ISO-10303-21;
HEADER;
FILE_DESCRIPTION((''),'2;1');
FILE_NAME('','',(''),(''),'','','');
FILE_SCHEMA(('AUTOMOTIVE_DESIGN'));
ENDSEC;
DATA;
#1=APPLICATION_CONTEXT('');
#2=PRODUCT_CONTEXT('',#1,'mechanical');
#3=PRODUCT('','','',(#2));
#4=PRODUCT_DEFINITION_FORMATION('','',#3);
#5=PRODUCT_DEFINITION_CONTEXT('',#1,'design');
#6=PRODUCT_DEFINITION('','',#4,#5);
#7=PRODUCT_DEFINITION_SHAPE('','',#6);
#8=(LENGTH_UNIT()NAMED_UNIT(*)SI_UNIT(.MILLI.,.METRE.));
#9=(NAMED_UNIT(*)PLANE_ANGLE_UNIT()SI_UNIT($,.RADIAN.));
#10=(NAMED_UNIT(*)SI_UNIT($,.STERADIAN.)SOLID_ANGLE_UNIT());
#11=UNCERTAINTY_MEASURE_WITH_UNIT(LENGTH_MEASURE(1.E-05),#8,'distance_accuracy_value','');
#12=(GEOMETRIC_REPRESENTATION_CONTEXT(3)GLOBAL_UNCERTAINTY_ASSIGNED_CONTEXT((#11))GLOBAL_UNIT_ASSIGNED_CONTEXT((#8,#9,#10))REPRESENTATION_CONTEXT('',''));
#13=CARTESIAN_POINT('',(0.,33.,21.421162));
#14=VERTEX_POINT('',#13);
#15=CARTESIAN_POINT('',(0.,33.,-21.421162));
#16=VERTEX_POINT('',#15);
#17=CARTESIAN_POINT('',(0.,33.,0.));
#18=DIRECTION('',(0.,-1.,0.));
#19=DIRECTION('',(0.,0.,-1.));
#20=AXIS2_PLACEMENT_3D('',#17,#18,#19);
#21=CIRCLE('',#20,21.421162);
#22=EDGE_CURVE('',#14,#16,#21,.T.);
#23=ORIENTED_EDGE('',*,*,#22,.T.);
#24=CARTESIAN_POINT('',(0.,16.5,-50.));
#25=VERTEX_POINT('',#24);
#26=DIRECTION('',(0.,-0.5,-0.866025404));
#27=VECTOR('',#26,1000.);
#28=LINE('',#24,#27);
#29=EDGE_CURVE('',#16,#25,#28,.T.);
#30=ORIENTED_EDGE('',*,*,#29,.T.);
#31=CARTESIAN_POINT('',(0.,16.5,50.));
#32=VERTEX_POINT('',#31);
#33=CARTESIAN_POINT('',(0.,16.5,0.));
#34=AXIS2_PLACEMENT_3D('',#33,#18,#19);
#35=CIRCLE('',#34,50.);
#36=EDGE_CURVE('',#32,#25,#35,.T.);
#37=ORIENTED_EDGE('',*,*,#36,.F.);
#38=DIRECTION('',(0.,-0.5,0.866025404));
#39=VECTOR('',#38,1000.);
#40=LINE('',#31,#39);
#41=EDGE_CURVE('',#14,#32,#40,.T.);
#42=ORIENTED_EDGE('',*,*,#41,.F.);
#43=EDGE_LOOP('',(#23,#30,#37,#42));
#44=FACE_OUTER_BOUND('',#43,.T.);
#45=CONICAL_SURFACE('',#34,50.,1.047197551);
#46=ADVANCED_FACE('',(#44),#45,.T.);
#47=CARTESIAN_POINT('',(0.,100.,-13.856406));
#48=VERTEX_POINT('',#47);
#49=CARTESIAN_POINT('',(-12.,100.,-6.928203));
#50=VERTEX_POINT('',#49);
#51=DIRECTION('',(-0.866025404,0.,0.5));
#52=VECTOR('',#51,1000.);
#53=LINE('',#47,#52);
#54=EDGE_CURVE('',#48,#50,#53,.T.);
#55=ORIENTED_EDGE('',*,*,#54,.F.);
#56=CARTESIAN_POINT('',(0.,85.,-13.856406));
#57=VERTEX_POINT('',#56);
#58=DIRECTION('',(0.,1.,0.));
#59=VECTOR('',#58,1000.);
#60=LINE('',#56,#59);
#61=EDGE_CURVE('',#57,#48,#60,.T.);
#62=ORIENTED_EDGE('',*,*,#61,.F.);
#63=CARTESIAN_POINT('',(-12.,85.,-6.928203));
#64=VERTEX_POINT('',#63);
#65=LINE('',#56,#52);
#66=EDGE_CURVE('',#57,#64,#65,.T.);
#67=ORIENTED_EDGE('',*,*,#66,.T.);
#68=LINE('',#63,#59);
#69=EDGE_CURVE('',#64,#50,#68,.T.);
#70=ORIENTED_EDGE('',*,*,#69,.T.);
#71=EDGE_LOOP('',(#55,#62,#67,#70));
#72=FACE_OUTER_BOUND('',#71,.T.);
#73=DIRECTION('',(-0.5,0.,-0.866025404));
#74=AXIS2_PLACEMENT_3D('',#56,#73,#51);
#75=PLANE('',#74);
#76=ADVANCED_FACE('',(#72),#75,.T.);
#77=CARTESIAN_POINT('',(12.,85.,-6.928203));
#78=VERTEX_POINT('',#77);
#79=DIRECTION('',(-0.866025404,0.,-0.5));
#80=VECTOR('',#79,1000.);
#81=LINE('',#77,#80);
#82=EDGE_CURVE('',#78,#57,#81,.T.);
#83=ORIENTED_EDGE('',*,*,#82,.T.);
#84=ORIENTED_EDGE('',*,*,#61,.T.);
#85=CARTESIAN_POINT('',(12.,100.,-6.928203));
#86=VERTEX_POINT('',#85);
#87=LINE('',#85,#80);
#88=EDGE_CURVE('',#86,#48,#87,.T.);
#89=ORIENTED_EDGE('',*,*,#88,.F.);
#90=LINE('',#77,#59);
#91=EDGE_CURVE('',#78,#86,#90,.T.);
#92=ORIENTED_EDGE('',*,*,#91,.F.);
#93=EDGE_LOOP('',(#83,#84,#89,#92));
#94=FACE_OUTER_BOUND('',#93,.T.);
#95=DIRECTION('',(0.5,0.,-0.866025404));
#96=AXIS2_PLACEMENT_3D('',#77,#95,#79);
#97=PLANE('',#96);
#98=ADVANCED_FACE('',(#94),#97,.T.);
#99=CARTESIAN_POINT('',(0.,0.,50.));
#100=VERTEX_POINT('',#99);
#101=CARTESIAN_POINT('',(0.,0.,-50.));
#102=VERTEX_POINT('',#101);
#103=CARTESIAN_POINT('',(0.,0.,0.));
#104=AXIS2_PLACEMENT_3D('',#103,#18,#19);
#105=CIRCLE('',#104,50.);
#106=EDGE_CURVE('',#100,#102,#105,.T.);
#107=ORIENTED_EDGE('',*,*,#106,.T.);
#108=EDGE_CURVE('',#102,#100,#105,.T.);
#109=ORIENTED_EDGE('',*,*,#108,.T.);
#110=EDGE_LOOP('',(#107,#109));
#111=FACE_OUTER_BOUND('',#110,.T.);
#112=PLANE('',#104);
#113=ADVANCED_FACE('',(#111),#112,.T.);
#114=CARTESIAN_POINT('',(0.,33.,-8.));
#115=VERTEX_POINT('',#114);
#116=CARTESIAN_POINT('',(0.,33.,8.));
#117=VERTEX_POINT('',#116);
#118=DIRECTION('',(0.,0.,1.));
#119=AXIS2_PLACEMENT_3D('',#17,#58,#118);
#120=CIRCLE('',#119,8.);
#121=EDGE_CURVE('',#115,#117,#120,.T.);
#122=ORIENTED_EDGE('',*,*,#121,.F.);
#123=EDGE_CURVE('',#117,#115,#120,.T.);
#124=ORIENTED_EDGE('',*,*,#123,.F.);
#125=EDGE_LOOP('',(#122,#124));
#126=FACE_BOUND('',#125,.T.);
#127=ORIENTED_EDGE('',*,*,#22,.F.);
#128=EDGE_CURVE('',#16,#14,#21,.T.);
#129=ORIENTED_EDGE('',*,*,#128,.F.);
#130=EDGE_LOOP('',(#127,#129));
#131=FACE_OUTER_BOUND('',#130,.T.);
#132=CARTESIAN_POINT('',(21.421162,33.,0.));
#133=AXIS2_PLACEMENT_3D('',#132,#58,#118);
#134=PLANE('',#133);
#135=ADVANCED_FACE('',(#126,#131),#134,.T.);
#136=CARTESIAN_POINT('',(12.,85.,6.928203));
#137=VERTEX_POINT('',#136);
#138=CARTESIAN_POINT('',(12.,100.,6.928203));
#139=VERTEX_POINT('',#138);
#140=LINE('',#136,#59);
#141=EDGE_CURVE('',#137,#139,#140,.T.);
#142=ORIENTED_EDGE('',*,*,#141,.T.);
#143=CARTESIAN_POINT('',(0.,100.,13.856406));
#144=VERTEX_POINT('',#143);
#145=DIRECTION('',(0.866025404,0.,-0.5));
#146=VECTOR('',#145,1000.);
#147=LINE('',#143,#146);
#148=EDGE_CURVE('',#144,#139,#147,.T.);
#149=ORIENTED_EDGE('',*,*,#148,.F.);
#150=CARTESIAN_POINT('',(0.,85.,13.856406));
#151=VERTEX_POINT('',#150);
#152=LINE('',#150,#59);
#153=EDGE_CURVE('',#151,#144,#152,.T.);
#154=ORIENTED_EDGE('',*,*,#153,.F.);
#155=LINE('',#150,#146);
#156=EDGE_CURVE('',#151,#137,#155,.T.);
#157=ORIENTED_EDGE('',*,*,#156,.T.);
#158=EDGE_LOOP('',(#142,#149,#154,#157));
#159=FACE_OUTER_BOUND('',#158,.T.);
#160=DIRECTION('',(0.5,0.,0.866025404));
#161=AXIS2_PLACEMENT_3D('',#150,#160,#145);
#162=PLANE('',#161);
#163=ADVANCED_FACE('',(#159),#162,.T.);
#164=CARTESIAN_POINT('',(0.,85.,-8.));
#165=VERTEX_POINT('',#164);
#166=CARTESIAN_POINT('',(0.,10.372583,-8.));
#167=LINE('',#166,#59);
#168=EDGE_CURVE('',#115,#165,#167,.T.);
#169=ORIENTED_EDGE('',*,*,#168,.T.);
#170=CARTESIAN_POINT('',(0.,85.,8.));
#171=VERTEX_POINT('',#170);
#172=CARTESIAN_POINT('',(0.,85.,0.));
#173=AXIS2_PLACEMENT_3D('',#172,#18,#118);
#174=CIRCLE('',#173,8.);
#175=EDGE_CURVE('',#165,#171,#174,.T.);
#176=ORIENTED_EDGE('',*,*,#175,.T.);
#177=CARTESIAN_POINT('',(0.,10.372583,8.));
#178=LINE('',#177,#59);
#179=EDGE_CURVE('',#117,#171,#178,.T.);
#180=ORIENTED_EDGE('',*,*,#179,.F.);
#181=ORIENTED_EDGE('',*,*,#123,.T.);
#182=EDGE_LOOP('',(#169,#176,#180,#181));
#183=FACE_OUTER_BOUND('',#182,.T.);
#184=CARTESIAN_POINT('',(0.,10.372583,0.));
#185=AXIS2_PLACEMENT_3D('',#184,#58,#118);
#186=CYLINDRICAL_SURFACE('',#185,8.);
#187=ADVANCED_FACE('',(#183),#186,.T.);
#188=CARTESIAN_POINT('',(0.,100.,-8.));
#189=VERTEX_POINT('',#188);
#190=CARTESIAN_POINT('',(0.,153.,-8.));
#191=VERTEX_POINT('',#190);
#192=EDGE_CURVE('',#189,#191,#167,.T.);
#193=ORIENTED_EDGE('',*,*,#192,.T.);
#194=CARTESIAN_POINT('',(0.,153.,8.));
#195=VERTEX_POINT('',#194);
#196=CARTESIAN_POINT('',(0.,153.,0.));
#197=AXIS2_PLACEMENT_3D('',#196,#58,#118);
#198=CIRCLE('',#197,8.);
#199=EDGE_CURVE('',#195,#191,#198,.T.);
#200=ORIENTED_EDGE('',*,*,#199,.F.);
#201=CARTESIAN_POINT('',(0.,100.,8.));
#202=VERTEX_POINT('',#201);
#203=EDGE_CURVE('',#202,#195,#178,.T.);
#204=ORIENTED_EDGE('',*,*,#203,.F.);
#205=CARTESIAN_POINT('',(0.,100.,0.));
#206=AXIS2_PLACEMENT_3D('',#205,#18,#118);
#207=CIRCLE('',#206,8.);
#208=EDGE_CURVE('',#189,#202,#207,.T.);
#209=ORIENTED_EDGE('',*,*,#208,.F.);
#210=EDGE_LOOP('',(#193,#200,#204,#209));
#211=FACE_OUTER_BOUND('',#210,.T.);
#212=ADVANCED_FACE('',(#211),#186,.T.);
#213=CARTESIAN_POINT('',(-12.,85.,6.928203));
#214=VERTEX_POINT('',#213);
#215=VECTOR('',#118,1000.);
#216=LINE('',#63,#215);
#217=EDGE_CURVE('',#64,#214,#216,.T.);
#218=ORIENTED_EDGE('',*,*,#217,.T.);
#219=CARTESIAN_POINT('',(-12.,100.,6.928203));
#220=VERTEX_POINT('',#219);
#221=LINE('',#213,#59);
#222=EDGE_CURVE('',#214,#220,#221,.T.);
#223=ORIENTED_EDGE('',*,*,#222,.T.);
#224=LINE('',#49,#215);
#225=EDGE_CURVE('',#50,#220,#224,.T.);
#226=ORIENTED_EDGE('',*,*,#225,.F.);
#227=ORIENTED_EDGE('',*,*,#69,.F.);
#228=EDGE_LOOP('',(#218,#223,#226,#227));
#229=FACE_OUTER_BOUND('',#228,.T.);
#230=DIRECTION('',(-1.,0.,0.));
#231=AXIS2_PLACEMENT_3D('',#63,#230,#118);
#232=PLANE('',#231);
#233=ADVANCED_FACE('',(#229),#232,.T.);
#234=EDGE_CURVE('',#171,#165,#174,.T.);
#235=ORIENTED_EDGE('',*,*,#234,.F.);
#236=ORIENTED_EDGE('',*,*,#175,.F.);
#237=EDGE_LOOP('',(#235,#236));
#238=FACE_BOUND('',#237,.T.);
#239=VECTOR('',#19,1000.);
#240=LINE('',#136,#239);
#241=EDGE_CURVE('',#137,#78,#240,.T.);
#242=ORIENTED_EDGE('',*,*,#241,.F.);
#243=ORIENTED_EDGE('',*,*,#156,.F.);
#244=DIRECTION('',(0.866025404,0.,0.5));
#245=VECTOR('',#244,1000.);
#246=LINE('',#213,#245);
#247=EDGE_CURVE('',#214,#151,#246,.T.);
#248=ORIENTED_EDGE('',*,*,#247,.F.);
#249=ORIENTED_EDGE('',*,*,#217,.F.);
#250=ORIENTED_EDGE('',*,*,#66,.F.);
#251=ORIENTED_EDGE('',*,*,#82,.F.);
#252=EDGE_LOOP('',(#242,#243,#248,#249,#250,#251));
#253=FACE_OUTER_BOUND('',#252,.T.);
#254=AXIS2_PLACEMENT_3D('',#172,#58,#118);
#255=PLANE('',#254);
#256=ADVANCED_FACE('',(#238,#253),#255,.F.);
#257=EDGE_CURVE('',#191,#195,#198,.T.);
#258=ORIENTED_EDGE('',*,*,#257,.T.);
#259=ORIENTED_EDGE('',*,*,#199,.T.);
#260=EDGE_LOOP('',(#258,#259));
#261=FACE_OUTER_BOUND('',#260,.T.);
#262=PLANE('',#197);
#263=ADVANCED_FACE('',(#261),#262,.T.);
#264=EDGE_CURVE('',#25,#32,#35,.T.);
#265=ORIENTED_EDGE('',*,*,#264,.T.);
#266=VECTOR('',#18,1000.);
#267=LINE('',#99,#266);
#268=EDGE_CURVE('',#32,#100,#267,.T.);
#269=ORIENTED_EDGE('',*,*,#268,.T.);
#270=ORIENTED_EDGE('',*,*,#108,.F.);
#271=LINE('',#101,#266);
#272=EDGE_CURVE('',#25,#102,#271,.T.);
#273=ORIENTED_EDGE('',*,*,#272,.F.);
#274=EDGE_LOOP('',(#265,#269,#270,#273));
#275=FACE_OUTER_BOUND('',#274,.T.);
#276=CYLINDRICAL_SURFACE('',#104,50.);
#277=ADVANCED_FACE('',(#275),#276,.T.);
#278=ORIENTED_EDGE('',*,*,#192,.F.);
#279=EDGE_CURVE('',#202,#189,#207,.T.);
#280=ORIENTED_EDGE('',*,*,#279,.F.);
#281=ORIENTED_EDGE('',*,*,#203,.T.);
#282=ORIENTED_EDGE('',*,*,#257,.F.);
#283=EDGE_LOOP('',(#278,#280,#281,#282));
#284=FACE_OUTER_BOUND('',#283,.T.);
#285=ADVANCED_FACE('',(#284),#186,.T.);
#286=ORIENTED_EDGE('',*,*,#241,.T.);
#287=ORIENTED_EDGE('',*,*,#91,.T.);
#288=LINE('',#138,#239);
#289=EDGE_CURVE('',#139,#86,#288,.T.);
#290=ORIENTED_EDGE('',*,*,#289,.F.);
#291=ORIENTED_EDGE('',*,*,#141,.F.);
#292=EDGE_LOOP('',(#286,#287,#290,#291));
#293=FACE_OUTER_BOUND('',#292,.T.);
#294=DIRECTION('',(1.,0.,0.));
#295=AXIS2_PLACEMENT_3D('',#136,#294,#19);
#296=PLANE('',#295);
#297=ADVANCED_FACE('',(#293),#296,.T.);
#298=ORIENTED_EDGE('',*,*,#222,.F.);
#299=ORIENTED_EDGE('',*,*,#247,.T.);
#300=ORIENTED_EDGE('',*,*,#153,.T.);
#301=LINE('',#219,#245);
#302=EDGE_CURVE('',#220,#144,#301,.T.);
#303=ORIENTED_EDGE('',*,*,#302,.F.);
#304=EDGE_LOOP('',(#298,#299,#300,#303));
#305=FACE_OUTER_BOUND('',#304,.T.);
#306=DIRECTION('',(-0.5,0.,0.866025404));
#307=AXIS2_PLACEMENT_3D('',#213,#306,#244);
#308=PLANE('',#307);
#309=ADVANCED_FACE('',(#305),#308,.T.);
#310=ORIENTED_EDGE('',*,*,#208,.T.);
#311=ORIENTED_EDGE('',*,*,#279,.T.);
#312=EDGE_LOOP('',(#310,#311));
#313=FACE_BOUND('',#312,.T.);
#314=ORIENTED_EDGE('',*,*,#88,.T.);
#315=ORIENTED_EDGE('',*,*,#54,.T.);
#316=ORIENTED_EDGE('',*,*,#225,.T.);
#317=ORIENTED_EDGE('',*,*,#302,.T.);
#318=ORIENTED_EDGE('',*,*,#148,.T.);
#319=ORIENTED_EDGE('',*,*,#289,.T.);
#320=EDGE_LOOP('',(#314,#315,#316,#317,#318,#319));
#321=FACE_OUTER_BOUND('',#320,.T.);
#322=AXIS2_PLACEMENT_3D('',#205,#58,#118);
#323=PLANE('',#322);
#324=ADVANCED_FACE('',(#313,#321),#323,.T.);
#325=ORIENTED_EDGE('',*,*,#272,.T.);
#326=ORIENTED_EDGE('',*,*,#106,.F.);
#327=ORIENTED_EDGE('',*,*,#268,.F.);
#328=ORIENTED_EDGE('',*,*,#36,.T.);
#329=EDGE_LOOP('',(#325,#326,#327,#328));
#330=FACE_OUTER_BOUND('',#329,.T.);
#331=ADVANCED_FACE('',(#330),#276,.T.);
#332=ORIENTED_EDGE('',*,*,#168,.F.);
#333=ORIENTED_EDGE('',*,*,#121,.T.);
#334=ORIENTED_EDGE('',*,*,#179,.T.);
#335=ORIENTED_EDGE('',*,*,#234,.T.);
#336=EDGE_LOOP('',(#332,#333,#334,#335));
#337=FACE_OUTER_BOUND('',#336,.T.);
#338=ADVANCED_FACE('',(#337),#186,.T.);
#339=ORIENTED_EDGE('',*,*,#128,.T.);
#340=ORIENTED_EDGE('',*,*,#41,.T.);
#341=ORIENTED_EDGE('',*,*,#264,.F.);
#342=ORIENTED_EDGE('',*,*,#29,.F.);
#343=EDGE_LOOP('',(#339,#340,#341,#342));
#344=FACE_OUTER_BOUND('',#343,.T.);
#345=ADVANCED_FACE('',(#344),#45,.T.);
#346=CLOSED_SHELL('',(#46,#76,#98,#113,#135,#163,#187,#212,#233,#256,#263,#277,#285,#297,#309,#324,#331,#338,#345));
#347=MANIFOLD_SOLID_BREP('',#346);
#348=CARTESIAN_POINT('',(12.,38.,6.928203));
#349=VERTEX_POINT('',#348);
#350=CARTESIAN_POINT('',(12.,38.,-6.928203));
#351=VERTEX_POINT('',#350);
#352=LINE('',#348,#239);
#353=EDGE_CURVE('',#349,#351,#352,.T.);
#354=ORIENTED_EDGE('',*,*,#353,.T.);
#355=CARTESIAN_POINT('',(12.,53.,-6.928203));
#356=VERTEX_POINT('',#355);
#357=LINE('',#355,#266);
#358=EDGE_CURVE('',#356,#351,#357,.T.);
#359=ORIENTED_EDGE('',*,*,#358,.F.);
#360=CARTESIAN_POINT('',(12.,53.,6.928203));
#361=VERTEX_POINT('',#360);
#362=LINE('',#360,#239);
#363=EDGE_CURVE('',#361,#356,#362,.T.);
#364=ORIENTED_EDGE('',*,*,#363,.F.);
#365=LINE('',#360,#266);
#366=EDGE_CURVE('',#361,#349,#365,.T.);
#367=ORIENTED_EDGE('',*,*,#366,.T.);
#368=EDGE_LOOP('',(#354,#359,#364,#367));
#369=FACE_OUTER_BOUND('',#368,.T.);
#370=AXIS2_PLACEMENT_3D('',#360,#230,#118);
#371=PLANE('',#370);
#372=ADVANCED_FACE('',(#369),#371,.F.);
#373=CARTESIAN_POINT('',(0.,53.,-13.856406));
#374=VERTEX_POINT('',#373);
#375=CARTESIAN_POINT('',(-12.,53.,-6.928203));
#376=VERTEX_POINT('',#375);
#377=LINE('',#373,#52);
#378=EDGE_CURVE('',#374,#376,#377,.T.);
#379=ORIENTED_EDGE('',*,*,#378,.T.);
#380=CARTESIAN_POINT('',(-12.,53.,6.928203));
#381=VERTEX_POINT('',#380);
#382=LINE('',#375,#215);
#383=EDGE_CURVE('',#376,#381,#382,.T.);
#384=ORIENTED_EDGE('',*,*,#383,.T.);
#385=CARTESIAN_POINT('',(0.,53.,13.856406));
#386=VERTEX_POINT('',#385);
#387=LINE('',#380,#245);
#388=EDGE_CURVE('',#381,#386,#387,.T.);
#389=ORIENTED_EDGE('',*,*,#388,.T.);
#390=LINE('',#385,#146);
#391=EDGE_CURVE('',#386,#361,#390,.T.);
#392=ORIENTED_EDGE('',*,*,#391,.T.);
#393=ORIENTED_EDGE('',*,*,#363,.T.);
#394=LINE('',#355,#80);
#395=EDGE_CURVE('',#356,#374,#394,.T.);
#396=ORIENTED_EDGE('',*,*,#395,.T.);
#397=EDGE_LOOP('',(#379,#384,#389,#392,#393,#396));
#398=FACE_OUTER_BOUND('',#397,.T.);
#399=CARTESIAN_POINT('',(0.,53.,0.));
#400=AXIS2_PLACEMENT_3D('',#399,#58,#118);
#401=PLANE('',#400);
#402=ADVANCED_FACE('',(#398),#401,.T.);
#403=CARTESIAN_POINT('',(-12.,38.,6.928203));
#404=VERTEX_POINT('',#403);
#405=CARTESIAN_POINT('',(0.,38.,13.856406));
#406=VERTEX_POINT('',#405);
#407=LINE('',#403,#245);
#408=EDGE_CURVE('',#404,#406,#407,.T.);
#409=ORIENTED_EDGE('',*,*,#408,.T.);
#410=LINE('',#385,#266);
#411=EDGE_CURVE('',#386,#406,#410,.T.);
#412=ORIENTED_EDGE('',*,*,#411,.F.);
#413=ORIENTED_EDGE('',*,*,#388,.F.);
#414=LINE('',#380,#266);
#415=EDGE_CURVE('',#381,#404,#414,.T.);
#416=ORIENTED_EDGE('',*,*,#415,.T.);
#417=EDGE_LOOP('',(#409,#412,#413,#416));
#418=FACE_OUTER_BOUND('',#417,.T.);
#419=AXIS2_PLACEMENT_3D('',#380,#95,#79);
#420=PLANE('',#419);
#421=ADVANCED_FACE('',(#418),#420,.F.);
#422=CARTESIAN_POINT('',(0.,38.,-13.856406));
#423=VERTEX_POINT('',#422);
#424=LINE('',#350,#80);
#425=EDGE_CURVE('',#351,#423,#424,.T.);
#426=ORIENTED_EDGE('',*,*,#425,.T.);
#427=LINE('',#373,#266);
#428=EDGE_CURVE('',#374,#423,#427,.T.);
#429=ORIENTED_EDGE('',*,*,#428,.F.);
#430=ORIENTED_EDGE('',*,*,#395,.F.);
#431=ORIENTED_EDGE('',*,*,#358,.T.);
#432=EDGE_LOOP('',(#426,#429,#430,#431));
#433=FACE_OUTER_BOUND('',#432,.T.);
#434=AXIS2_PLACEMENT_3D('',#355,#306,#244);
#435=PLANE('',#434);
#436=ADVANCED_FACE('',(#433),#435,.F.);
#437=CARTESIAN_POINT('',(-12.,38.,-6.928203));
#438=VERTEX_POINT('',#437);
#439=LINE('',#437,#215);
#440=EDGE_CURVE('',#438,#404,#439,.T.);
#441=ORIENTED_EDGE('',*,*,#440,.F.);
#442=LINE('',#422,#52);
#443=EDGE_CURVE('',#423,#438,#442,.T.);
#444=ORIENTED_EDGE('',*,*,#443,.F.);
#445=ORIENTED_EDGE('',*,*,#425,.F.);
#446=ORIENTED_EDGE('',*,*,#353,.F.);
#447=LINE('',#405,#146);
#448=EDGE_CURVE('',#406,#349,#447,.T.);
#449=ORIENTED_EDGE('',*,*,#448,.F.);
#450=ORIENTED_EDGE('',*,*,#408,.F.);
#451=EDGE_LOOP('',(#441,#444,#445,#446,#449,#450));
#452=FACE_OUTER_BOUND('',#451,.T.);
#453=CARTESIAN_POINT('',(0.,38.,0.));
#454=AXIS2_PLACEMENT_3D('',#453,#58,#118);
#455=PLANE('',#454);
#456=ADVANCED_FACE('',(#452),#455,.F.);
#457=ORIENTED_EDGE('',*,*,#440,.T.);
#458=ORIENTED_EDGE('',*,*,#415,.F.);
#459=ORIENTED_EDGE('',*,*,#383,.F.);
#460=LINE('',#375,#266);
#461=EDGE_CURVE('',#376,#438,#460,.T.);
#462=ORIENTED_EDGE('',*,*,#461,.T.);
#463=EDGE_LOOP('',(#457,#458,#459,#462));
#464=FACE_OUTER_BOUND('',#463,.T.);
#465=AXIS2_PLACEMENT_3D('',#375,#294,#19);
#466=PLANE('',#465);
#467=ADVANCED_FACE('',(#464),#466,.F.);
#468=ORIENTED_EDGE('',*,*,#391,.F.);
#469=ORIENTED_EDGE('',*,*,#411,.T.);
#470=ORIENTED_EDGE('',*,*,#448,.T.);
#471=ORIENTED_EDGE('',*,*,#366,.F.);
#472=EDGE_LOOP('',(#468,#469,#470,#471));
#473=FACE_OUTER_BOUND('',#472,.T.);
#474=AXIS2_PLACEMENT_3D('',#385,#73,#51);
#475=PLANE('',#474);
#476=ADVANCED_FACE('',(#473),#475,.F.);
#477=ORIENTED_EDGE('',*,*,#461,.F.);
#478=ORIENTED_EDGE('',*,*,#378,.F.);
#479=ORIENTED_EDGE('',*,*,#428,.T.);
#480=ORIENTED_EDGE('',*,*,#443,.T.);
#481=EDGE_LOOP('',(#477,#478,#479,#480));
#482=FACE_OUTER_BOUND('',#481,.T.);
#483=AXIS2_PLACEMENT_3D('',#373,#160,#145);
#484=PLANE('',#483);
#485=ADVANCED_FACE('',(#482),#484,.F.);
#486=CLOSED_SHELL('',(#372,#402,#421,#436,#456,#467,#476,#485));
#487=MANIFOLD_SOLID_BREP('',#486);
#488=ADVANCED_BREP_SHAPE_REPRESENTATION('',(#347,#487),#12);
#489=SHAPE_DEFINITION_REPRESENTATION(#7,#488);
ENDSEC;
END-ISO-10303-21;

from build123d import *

# Parameters (mm, degrees)
EXTRUDE_START        = 5
EXTRUDE_1_DEPTH      = 15
EXTRUDE_2_DEPTH      = 100
EXTRUDE_2_DEPTH_BACK = 53
SKETCH_3_R           = 8
EXTRUDE_START_2      = 100
EXTRUDE_3_DEPTH      = 15


with BuildPart() as part:
    # 草图1 → 旋转1 (revolve)
    with BuildSketch(Plane.XY, mode=Mode.PRIVATE) as revolve_1_sk:
        Polygon((0, 0), (50, 0), (50, 16.5), (21.421161675, 33), (0, 33), align=None)
    revolve(revolve_1_sk.sketch.rotate(Axis((0, 0, 0), (0, 1, 0)), 90), axis=Axis((0, 0, 0), (0, 1, 0)))

    # 草图3 → 凸台-拉伸2 (add, two sides: drawn at the far end of the back side and taken through both)
    with BuildSketch(Plane(origin=(0, 53, 0), x_dir=(1, 0, 0), z_dir=(0, 1, 0)).offset(-EXTRUDE_2_DEPTH_BACK)):
        with Locations(Location((0, 0, 0), (0, 0, 270))):
            Circle(SKETCH_3_R)
    extrude(amount=EXTRUDE_2_DEPTH + EXTRUDE_2_DEPTH_BACK)

    # 草图4 → 凸台-拉伸3 (add)
    with BuildSketch(Plane(origin=(0, 0, 0), x_dir=(1, 0, 0), z_dir=(0, 1, 0)).offset(EXTRUDE_START_2)):
        Polygon((0, -13.856406461), (12, -6.92820323), (12, 6.92820323), (0, 13.856406461), (-12, 6.92820323), (-12, -6.92820323), align=None)
    extrude(amount=-EXTRUDE_3_DEPTH)


with BuildPart() as body_2:
    # 草图2 → 凸台-拉伸1 (new body)
    with BuildSketch(Plane(origin=(0, 33, 0), x_dir=(1, 0, 0), z_dir=(0, 1, 0)).offset(EXTRUDE_START)):
        Polygon((12, -6.92820323), (12, 6.92820323), (0, 13.856406461), (-12, 6.92820323), (-12, -6.92820323), (0, -13.856406461), align=None)
    extrude(amount=EXTRUDE_1_DEPTH)


solid = Compound([part.part, body_2.part])
